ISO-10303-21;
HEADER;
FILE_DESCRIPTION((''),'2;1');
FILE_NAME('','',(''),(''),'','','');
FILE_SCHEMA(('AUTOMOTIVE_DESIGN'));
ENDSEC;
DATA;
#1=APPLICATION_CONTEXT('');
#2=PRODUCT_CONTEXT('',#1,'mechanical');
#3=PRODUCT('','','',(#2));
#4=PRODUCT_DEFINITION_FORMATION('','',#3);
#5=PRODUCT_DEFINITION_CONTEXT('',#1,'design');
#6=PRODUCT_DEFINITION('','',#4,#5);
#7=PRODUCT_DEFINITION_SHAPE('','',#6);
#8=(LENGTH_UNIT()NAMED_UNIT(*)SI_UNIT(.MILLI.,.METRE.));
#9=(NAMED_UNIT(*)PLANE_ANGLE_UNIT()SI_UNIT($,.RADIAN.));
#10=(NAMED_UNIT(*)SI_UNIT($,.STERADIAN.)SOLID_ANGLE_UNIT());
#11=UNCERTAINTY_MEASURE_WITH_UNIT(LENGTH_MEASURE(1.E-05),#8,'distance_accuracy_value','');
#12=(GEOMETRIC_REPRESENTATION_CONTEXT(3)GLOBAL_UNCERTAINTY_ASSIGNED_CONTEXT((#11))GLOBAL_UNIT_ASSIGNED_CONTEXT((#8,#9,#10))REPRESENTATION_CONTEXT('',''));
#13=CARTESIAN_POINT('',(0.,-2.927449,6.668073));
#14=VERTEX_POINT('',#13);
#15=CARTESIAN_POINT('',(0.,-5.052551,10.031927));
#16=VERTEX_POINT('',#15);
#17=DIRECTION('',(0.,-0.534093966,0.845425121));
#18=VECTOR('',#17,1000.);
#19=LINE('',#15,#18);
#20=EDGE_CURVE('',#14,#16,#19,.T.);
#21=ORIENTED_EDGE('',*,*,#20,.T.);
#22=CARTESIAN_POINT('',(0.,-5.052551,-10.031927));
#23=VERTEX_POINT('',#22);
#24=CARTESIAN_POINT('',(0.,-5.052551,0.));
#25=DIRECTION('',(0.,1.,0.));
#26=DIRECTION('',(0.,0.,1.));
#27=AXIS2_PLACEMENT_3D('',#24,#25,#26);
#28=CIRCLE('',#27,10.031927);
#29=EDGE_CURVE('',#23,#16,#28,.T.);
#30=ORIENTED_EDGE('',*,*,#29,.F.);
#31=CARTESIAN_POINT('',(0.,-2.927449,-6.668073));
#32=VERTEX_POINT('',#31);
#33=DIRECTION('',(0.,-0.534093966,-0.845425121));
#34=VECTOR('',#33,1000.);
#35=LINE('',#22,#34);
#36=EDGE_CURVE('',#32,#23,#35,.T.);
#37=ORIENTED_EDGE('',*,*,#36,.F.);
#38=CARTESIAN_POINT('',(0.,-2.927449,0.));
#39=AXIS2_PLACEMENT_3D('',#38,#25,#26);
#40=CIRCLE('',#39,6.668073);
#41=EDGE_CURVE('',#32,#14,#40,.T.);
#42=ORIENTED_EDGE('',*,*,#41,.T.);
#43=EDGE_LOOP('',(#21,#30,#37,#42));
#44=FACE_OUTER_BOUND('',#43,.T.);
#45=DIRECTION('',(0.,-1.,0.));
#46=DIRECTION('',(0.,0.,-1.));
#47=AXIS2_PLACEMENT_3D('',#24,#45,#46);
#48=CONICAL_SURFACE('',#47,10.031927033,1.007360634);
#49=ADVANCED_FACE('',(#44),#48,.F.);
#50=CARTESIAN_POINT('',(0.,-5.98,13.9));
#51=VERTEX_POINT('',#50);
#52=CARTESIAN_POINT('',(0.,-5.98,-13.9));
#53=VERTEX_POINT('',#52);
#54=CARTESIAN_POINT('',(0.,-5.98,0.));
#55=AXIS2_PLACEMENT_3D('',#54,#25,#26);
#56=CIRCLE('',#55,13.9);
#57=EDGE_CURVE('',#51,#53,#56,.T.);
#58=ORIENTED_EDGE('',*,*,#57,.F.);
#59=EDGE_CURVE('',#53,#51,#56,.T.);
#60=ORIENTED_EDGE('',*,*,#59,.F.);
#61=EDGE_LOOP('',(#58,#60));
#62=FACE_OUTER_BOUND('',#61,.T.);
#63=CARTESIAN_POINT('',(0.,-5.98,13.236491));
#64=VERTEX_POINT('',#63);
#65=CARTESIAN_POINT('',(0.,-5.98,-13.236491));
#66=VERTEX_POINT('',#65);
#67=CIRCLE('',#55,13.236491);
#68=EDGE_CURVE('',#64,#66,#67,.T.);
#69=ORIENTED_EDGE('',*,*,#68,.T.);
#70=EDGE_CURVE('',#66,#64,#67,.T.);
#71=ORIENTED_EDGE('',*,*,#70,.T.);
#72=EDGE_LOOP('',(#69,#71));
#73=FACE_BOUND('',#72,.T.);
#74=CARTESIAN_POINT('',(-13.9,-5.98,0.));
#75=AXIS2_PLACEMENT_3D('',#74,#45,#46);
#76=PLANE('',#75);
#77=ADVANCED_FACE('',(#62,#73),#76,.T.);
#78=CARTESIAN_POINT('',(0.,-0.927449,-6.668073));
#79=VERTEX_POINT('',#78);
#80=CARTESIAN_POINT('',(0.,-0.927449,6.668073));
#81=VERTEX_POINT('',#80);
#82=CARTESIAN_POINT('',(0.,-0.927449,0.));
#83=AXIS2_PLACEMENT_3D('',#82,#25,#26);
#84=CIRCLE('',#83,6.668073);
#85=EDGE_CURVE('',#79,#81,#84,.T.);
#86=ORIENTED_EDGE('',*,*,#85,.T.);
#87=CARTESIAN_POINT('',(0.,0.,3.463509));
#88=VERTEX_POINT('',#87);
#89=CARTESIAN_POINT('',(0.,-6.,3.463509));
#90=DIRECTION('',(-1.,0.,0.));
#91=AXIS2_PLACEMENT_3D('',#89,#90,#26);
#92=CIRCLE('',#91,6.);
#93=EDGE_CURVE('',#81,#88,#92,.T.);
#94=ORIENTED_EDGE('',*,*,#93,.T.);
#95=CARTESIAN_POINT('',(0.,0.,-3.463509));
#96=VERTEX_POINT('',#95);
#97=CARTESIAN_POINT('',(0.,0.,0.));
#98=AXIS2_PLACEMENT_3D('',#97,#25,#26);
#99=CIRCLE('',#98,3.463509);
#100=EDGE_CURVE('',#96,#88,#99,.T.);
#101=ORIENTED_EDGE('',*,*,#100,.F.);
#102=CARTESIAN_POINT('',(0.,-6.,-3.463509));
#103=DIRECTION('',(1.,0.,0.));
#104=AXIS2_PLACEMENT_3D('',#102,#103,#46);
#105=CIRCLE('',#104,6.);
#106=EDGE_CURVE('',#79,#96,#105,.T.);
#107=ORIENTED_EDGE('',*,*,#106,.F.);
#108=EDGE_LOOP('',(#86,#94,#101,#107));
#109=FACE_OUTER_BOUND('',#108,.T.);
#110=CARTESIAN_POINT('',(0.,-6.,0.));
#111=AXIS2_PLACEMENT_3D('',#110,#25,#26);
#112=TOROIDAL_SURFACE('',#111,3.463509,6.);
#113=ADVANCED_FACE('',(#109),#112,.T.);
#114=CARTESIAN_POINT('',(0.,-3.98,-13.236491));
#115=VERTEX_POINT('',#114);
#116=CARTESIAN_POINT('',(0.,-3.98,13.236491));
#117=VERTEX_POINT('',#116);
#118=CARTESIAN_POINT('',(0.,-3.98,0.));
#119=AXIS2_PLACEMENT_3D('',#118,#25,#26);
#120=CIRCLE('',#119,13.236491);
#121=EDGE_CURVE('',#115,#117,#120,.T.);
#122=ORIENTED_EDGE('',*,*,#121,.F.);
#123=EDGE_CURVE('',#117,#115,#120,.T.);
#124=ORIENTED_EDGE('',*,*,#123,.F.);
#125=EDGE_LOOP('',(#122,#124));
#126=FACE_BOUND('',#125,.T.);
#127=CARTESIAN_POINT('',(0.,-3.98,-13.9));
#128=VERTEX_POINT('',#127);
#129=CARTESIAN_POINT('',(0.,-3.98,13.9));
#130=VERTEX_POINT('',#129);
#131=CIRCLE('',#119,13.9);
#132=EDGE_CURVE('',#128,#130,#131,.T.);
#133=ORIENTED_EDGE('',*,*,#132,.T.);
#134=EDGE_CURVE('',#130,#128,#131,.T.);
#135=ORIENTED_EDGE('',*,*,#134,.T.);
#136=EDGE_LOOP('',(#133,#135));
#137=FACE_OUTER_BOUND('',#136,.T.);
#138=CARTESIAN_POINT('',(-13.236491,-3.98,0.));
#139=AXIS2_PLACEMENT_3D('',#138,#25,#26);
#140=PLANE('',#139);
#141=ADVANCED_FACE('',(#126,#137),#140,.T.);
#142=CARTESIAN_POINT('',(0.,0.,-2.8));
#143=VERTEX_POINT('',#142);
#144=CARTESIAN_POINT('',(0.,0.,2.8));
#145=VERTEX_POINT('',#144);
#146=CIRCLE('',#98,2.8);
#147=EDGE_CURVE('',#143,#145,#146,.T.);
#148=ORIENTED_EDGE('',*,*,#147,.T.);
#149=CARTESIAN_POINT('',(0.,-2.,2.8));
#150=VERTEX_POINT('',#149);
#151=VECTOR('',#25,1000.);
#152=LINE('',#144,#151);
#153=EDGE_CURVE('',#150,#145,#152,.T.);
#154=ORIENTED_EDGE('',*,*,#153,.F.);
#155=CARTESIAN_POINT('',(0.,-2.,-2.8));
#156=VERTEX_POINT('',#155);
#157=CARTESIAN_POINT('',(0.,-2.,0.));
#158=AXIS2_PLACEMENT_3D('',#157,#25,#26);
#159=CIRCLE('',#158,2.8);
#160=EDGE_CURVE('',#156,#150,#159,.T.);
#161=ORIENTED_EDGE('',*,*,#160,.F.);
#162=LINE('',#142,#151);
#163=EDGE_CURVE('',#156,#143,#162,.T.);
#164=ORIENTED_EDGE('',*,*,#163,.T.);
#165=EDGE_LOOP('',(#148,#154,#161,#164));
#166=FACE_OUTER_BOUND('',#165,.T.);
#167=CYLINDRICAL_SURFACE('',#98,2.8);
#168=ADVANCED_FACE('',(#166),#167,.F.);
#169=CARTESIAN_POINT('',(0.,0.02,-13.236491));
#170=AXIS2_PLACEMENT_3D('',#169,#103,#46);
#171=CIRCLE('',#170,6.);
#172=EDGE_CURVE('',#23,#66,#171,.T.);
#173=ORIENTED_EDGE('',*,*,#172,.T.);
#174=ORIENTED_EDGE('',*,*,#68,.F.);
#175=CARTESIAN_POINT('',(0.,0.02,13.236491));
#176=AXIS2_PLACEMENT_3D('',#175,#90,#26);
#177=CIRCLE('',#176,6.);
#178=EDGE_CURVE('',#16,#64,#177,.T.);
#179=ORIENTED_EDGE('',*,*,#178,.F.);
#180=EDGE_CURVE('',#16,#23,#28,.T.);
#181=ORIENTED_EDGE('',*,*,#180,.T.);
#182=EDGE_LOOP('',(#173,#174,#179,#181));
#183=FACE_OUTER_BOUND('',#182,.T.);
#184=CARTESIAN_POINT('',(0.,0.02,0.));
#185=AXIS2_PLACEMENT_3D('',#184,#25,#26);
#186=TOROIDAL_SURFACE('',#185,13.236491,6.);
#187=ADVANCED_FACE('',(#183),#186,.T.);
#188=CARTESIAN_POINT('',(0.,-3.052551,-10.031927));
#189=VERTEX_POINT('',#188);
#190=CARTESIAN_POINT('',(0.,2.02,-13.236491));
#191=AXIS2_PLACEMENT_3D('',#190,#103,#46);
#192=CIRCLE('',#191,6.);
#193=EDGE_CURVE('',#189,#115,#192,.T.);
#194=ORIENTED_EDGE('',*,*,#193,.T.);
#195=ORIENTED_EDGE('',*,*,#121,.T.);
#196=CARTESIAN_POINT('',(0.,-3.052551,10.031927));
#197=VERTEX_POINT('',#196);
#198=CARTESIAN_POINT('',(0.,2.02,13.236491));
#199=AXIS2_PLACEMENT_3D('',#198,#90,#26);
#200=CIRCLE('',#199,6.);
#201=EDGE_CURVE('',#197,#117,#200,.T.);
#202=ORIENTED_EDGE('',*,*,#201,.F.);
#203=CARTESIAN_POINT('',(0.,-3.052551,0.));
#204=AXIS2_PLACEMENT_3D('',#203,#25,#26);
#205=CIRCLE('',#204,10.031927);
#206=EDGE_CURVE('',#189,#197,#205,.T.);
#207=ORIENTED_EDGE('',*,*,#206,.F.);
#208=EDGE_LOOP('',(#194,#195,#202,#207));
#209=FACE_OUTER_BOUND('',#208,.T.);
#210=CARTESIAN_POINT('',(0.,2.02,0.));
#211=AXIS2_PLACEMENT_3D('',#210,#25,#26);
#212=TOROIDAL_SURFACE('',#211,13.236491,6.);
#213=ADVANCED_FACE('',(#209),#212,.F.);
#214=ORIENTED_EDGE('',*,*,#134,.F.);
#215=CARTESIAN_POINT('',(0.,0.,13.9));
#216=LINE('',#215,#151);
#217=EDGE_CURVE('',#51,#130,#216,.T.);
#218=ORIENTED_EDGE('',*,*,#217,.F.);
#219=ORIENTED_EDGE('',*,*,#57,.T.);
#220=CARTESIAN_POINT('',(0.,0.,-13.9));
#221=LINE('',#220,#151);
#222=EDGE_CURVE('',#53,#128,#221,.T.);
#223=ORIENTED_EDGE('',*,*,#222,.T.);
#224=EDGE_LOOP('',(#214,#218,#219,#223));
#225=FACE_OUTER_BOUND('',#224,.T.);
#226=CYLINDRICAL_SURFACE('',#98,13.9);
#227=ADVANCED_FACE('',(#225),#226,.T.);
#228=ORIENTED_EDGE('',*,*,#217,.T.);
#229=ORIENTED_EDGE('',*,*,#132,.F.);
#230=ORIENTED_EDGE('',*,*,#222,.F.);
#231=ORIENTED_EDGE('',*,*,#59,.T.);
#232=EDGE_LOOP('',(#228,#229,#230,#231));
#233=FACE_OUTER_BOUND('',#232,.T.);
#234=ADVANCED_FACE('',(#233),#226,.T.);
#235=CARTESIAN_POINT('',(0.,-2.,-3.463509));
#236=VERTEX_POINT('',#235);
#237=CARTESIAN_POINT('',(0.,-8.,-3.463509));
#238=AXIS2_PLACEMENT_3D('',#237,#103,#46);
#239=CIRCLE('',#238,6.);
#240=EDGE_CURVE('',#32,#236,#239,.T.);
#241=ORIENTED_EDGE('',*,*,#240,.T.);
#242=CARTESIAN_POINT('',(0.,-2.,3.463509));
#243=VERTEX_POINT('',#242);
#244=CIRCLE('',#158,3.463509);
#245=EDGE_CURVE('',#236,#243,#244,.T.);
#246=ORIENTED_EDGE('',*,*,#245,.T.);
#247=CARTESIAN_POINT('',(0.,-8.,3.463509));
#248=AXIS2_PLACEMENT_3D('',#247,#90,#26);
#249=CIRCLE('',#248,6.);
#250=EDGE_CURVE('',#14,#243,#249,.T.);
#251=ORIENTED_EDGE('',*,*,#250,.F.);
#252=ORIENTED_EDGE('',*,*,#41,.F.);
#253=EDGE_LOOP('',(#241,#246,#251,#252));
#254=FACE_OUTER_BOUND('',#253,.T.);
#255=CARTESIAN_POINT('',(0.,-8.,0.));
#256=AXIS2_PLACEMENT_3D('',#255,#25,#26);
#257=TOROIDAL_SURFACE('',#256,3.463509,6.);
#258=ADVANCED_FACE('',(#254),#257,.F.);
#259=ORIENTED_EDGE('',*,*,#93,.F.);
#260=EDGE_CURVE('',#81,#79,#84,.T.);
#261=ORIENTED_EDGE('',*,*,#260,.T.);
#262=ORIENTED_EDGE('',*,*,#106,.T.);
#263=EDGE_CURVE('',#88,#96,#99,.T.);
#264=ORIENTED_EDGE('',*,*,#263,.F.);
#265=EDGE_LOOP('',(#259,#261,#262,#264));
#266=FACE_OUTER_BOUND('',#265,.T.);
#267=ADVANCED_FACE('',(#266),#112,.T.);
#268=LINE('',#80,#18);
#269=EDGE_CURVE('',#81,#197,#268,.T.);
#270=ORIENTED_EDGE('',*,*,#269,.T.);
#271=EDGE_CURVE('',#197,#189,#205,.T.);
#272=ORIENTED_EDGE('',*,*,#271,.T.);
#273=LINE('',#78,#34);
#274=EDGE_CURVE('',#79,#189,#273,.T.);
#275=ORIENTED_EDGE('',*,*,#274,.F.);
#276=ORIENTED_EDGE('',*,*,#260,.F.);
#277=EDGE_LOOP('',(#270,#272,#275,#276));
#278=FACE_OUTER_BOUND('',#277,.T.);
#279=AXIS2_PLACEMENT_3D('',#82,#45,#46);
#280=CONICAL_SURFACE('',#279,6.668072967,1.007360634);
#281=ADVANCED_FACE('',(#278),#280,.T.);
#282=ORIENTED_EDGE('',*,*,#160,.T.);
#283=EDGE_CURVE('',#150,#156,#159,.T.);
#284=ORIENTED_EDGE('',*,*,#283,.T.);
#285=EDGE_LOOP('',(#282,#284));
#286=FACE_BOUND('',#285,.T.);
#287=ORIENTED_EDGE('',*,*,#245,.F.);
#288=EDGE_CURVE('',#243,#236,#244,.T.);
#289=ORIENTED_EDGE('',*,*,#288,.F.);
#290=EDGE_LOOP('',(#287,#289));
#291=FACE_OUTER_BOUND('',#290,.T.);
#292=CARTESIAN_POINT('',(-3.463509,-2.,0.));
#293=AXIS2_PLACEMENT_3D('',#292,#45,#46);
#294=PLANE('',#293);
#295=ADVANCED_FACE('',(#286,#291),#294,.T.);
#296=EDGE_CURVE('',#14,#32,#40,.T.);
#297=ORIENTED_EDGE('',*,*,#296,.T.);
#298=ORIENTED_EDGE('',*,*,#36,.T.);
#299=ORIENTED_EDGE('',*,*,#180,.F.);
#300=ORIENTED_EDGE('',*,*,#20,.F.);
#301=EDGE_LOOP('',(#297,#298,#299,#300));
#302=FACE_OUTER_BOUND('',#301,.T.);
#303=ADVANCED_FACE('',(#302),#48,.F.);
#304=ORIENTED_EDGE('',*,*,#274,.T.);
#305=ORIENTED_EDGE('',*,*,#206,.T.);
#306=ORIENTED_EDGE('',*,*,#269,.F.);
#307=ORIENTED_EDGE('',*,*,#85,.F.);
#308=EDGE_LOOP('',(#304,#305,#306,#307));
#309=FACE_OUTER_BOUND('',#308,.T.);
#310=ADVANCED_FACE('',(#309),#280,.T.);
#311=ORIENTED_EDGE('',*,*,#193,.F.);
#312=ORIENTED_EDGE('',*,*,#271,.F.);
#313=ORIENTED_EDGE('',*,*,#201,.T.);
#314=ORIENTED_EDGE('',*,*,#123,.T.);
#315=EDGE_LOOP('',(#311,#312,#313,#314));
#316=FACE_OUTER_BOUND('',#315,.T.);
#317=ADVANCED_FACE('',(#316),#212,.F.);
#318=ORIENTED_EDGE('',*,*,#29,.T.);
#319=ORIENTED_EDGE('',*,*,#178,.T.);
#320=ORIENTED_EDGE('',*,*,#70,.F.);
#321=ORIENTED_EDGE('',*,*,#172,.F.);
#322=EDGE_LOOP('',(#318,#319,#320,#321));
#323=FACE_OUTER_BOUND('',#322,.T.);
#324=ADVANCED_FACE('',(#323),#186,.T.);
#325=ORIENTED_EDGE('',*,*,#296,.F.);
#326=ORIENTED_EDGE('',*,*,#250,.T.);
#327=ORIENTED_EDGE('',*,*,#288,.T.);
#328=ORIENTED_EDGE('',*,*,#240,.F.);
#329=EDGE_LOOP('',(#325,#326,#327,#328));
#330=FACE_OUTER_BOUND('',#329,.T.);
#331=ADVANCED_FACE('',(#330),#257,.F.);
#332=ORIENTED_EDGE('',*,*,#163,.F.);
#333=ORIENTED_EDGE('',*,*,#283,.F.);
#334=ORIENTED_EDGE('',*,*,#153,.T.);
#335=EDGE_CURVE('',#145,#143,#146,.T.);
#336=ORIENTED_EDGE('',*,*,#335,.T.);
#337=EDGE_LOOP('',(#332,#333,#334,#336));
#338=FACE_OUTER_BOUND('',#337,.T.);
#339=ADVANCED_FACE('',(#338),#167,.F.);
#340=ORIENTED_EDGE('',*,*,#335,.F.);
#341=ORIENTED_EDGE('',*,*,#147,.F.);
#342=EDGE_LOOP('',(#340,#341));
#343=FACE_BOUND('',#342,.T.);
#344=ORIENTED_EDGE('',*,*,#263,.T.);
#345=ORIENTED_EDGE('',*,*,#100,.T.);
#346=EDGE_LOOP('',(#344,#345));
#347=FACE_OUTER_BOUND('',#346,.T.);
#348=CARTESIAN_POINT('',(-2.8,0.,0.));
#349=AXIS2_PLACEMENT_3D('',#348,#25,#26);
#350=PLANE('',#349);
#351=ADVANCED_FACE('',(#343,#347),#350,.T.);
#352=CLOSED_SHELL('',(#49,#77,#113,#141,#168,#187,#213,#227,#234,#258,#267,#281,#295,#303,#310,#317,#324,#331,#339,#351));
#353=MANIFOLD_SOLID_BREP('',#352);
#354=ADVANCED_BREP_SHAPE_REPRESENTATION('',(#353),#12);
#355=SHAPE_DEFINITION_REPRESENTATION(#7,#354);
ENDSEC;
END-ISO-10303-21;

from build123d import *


with BuildPart() as part:
    # Sketch1 → Revolve1 (revolve)
    with BuildSketch(Plane.XY, mode=Mode.PRIVATE) as revolve1_sk:
        with BuildLine():
            Line((-2.8, 0), (-3.463509174, 0))
            ThreePointArc((-3.463509174, 0), (-5.131546288, -0.236524296), (-6.668072967, -0.927449272))
            Line((-6.668072967, -0.927449272), (-10.031927033, -3.052550728))
            ThreePointArc((-10.031927033, -3.052550728), (-11.568453712, -3.743475704), (-13.236490826, -3.98))
            Line((-13.236490826, -3.98), (-13.9, -3.98))
            Line((-13.9, -3.98), (-13.9, -5.98))
            Line((-13.9, -5.98), (-13.236490826, -5.98))
            ThreePointArc((-13.236490826, -5.98), (-11.568453712, -5.743475704), (-10.031927033, -5.052550728))
            Line((-10.031927033, -5.052550728), (-6.668072967, -2.927449272))
            ThreePointArc((-6.668072967, -2.927449272), (-5.131546288, -2.236524296), (-3.463509174, -2))
            Line((-3.463509174, -2), (-2.8, -2))
            Line((-2.8, -2), (-2.8, 0))
        make_face()
    revolve(revolve1_sk.sketch.rotate(Axis((0, 0, 0), (0, -1, 0)), 270), axis=Axis((0, 0, 0), (0, -1, 0)))


solid = part.part
